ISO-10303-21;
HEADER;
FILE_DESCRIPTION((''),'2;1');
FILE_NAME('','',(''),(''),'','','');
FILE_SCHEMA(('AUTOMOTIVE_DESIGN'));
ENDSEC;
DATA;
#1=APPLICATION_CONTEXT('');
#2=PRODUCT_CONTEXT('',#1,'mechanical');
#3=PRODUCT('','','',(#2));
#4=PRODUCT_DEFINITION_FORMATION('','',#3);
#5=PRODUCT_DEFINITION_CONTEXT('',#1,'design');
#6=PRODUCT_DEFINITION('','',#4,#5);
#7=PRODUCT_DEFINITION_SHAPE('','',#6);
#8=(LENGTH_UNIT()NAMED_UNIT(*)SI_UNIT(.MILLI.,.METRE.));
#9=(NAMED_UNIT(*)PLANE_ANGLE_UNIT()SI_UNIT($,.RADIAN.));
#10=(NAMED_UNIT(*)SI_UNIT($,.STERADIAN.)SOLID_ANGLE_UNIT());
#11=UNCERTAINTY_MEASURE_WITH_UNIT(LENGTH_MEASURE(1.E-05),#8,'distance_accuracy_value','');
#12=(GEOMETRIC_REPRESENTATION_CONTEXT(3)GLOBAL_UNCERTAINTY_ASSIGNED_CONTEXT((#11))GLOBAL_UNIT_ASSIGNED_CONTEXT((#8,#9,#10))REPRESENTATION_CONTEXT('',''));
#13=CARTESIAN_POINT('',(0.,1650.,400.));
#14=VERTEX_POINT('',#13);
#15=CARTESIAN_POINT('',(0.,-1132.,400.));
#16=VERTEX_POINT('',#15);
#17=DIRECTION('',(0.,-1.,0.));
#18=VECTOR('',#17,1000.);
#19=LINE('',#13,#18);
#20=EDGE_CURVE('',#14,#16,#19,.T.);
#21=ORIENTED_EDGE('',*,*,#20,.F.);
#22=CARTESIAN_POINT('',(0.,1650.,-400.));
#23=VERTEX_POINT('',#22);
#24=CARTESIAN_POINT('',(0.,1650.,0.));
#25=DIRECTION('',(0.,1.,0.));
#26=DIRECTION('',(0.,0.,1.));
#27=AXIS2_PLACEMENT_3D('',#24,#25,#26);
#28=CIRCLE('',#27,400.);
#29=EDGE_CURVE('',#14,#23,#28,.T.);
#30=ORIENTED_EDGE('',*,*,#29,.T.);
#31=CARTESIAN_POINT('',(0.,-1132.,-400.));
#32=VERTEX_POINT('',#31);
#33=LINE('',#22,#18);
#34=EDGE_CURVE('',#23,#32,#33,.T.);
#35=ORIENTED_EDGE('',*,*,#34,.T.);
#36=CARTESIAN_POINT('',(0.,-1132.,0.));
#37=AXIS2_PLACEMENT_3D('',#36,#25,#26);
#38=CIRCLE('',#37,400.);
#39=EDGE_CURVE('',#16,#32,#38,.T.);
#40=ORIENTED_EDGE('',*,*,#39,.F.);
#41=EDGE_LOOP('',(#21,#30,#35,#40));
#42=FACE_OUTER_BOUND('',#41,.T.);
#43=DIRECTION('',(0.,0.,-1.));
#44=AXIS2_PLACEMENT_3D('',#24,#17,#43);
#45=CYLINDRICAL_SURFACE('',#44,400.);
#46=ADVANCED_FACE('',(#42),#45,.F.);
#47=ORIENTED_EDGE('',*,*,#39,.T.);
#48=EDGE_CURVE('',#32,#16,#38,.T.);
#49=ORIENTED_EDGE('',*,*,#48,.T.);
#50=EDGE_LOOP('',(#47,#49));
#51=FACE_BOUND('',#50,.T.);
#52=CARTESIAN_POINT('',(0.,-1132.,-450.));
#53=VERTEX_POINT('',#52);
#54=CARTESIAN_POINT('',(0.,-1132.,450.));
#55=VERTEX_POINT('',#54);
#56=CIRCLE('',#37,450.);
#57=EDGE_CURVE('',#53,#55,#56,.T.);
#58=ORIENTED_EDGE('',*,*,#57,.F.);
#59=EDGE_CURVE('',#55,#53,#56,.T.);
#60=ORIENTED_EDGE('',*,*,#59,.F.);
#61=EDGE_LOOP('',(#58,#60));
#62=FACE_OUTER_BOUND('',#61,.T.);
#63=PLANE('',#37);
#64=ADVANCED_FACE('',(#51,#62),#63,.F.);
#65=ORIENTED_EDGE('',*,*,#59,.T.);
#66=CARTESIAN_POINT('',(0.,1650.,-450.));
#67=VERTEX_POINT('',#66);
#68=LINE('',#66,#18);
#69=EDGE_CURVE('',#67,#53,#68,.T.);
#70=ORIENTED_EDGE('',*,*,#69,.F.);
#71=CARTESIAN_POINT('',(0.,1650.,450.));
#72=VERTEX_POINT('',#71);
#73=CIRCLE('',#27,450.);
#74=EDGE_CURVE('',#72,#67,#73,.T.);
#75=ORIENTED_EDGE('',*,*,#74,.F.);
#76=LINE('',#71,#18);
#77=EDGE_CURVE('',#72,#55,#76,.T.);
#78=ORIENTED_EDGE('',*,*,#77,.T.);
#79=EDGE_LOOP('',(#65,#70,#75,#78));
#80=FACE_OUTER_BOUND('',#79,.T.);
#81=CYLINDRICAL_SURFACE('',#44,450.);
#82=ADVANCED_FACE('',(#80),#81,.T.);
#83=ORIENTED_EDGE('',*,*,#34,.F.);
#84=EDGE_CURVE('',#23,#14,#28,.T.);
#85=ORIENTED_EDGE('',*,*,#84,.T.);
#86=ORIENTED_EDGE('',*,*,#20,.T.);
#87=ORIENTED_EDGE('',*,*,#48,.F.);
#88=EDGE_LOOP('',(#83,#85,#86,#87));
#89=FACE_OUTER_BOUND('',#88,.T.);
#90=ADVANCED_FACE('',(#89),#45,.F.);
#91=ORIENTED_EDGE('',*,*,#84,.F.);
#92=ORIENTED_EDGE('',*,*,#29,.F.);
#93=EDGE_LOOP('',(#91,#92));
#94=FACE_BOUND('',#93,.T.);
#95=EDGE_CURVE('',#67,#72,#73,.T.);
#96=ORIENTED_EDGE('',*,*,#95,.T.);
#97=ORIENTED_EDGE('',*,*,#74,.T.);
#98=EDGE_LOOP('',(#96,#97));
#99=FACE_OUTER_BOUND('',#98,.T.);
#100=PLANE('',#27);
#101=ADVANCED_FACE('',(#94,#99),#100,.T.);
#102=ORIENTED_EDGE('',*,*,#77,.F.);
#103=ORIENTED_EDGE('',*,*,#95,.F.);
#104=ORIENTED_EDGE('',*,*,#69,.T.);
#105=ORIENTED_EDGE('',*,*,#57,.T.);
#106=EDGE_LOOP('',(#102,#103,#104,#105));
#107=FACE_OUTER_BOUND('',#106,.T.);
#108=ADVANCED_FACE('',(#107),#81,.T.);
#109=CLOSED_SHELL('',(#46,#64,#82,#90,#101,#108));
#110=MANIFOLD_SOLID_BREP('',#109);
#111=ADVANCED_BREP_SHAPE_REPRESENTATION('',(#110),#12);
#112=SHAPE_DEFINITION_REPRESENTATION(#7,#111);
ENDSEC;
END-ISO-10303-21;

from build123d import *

# Parameters (mm, degrees)
SKETCH1_R           = 450
SKETCH1_R_2         = 400
BOSS_EXTRUDE1_DEPTH = 1650
MOVE_FACE1_BY       = 518


with BuildPart() as part:
    # Sketch1 → Boss-Extrude1 (new, symmetric)
    with BuildSketch(Plane(origin=(0, 0, 0), x_dir=(1, 0, 0), z_dir=(0, 1, 0))):
        with Locations(Location((0, 0, 0), (0, 0, 270))):
            Circle(SKETCH1_R)
        with Locations(Location((0, 0, 0), (0, 0, 270))):
            Circle(SKETCH1_R_2, mode=Mode.SUBTRACT)
    extrude(amount=BOSS_EXTRUDE1_DEPTH, both=True)

    # Move Face1: a face moved inward by 518.0
    extrude(part.faces().sort_by_distance((-225, -1650, 360))[0], amount=MOVE_FACE1_BY, dir=(0, 1, 0), mode=Mode.SUBTRACT)


solid = part.part
